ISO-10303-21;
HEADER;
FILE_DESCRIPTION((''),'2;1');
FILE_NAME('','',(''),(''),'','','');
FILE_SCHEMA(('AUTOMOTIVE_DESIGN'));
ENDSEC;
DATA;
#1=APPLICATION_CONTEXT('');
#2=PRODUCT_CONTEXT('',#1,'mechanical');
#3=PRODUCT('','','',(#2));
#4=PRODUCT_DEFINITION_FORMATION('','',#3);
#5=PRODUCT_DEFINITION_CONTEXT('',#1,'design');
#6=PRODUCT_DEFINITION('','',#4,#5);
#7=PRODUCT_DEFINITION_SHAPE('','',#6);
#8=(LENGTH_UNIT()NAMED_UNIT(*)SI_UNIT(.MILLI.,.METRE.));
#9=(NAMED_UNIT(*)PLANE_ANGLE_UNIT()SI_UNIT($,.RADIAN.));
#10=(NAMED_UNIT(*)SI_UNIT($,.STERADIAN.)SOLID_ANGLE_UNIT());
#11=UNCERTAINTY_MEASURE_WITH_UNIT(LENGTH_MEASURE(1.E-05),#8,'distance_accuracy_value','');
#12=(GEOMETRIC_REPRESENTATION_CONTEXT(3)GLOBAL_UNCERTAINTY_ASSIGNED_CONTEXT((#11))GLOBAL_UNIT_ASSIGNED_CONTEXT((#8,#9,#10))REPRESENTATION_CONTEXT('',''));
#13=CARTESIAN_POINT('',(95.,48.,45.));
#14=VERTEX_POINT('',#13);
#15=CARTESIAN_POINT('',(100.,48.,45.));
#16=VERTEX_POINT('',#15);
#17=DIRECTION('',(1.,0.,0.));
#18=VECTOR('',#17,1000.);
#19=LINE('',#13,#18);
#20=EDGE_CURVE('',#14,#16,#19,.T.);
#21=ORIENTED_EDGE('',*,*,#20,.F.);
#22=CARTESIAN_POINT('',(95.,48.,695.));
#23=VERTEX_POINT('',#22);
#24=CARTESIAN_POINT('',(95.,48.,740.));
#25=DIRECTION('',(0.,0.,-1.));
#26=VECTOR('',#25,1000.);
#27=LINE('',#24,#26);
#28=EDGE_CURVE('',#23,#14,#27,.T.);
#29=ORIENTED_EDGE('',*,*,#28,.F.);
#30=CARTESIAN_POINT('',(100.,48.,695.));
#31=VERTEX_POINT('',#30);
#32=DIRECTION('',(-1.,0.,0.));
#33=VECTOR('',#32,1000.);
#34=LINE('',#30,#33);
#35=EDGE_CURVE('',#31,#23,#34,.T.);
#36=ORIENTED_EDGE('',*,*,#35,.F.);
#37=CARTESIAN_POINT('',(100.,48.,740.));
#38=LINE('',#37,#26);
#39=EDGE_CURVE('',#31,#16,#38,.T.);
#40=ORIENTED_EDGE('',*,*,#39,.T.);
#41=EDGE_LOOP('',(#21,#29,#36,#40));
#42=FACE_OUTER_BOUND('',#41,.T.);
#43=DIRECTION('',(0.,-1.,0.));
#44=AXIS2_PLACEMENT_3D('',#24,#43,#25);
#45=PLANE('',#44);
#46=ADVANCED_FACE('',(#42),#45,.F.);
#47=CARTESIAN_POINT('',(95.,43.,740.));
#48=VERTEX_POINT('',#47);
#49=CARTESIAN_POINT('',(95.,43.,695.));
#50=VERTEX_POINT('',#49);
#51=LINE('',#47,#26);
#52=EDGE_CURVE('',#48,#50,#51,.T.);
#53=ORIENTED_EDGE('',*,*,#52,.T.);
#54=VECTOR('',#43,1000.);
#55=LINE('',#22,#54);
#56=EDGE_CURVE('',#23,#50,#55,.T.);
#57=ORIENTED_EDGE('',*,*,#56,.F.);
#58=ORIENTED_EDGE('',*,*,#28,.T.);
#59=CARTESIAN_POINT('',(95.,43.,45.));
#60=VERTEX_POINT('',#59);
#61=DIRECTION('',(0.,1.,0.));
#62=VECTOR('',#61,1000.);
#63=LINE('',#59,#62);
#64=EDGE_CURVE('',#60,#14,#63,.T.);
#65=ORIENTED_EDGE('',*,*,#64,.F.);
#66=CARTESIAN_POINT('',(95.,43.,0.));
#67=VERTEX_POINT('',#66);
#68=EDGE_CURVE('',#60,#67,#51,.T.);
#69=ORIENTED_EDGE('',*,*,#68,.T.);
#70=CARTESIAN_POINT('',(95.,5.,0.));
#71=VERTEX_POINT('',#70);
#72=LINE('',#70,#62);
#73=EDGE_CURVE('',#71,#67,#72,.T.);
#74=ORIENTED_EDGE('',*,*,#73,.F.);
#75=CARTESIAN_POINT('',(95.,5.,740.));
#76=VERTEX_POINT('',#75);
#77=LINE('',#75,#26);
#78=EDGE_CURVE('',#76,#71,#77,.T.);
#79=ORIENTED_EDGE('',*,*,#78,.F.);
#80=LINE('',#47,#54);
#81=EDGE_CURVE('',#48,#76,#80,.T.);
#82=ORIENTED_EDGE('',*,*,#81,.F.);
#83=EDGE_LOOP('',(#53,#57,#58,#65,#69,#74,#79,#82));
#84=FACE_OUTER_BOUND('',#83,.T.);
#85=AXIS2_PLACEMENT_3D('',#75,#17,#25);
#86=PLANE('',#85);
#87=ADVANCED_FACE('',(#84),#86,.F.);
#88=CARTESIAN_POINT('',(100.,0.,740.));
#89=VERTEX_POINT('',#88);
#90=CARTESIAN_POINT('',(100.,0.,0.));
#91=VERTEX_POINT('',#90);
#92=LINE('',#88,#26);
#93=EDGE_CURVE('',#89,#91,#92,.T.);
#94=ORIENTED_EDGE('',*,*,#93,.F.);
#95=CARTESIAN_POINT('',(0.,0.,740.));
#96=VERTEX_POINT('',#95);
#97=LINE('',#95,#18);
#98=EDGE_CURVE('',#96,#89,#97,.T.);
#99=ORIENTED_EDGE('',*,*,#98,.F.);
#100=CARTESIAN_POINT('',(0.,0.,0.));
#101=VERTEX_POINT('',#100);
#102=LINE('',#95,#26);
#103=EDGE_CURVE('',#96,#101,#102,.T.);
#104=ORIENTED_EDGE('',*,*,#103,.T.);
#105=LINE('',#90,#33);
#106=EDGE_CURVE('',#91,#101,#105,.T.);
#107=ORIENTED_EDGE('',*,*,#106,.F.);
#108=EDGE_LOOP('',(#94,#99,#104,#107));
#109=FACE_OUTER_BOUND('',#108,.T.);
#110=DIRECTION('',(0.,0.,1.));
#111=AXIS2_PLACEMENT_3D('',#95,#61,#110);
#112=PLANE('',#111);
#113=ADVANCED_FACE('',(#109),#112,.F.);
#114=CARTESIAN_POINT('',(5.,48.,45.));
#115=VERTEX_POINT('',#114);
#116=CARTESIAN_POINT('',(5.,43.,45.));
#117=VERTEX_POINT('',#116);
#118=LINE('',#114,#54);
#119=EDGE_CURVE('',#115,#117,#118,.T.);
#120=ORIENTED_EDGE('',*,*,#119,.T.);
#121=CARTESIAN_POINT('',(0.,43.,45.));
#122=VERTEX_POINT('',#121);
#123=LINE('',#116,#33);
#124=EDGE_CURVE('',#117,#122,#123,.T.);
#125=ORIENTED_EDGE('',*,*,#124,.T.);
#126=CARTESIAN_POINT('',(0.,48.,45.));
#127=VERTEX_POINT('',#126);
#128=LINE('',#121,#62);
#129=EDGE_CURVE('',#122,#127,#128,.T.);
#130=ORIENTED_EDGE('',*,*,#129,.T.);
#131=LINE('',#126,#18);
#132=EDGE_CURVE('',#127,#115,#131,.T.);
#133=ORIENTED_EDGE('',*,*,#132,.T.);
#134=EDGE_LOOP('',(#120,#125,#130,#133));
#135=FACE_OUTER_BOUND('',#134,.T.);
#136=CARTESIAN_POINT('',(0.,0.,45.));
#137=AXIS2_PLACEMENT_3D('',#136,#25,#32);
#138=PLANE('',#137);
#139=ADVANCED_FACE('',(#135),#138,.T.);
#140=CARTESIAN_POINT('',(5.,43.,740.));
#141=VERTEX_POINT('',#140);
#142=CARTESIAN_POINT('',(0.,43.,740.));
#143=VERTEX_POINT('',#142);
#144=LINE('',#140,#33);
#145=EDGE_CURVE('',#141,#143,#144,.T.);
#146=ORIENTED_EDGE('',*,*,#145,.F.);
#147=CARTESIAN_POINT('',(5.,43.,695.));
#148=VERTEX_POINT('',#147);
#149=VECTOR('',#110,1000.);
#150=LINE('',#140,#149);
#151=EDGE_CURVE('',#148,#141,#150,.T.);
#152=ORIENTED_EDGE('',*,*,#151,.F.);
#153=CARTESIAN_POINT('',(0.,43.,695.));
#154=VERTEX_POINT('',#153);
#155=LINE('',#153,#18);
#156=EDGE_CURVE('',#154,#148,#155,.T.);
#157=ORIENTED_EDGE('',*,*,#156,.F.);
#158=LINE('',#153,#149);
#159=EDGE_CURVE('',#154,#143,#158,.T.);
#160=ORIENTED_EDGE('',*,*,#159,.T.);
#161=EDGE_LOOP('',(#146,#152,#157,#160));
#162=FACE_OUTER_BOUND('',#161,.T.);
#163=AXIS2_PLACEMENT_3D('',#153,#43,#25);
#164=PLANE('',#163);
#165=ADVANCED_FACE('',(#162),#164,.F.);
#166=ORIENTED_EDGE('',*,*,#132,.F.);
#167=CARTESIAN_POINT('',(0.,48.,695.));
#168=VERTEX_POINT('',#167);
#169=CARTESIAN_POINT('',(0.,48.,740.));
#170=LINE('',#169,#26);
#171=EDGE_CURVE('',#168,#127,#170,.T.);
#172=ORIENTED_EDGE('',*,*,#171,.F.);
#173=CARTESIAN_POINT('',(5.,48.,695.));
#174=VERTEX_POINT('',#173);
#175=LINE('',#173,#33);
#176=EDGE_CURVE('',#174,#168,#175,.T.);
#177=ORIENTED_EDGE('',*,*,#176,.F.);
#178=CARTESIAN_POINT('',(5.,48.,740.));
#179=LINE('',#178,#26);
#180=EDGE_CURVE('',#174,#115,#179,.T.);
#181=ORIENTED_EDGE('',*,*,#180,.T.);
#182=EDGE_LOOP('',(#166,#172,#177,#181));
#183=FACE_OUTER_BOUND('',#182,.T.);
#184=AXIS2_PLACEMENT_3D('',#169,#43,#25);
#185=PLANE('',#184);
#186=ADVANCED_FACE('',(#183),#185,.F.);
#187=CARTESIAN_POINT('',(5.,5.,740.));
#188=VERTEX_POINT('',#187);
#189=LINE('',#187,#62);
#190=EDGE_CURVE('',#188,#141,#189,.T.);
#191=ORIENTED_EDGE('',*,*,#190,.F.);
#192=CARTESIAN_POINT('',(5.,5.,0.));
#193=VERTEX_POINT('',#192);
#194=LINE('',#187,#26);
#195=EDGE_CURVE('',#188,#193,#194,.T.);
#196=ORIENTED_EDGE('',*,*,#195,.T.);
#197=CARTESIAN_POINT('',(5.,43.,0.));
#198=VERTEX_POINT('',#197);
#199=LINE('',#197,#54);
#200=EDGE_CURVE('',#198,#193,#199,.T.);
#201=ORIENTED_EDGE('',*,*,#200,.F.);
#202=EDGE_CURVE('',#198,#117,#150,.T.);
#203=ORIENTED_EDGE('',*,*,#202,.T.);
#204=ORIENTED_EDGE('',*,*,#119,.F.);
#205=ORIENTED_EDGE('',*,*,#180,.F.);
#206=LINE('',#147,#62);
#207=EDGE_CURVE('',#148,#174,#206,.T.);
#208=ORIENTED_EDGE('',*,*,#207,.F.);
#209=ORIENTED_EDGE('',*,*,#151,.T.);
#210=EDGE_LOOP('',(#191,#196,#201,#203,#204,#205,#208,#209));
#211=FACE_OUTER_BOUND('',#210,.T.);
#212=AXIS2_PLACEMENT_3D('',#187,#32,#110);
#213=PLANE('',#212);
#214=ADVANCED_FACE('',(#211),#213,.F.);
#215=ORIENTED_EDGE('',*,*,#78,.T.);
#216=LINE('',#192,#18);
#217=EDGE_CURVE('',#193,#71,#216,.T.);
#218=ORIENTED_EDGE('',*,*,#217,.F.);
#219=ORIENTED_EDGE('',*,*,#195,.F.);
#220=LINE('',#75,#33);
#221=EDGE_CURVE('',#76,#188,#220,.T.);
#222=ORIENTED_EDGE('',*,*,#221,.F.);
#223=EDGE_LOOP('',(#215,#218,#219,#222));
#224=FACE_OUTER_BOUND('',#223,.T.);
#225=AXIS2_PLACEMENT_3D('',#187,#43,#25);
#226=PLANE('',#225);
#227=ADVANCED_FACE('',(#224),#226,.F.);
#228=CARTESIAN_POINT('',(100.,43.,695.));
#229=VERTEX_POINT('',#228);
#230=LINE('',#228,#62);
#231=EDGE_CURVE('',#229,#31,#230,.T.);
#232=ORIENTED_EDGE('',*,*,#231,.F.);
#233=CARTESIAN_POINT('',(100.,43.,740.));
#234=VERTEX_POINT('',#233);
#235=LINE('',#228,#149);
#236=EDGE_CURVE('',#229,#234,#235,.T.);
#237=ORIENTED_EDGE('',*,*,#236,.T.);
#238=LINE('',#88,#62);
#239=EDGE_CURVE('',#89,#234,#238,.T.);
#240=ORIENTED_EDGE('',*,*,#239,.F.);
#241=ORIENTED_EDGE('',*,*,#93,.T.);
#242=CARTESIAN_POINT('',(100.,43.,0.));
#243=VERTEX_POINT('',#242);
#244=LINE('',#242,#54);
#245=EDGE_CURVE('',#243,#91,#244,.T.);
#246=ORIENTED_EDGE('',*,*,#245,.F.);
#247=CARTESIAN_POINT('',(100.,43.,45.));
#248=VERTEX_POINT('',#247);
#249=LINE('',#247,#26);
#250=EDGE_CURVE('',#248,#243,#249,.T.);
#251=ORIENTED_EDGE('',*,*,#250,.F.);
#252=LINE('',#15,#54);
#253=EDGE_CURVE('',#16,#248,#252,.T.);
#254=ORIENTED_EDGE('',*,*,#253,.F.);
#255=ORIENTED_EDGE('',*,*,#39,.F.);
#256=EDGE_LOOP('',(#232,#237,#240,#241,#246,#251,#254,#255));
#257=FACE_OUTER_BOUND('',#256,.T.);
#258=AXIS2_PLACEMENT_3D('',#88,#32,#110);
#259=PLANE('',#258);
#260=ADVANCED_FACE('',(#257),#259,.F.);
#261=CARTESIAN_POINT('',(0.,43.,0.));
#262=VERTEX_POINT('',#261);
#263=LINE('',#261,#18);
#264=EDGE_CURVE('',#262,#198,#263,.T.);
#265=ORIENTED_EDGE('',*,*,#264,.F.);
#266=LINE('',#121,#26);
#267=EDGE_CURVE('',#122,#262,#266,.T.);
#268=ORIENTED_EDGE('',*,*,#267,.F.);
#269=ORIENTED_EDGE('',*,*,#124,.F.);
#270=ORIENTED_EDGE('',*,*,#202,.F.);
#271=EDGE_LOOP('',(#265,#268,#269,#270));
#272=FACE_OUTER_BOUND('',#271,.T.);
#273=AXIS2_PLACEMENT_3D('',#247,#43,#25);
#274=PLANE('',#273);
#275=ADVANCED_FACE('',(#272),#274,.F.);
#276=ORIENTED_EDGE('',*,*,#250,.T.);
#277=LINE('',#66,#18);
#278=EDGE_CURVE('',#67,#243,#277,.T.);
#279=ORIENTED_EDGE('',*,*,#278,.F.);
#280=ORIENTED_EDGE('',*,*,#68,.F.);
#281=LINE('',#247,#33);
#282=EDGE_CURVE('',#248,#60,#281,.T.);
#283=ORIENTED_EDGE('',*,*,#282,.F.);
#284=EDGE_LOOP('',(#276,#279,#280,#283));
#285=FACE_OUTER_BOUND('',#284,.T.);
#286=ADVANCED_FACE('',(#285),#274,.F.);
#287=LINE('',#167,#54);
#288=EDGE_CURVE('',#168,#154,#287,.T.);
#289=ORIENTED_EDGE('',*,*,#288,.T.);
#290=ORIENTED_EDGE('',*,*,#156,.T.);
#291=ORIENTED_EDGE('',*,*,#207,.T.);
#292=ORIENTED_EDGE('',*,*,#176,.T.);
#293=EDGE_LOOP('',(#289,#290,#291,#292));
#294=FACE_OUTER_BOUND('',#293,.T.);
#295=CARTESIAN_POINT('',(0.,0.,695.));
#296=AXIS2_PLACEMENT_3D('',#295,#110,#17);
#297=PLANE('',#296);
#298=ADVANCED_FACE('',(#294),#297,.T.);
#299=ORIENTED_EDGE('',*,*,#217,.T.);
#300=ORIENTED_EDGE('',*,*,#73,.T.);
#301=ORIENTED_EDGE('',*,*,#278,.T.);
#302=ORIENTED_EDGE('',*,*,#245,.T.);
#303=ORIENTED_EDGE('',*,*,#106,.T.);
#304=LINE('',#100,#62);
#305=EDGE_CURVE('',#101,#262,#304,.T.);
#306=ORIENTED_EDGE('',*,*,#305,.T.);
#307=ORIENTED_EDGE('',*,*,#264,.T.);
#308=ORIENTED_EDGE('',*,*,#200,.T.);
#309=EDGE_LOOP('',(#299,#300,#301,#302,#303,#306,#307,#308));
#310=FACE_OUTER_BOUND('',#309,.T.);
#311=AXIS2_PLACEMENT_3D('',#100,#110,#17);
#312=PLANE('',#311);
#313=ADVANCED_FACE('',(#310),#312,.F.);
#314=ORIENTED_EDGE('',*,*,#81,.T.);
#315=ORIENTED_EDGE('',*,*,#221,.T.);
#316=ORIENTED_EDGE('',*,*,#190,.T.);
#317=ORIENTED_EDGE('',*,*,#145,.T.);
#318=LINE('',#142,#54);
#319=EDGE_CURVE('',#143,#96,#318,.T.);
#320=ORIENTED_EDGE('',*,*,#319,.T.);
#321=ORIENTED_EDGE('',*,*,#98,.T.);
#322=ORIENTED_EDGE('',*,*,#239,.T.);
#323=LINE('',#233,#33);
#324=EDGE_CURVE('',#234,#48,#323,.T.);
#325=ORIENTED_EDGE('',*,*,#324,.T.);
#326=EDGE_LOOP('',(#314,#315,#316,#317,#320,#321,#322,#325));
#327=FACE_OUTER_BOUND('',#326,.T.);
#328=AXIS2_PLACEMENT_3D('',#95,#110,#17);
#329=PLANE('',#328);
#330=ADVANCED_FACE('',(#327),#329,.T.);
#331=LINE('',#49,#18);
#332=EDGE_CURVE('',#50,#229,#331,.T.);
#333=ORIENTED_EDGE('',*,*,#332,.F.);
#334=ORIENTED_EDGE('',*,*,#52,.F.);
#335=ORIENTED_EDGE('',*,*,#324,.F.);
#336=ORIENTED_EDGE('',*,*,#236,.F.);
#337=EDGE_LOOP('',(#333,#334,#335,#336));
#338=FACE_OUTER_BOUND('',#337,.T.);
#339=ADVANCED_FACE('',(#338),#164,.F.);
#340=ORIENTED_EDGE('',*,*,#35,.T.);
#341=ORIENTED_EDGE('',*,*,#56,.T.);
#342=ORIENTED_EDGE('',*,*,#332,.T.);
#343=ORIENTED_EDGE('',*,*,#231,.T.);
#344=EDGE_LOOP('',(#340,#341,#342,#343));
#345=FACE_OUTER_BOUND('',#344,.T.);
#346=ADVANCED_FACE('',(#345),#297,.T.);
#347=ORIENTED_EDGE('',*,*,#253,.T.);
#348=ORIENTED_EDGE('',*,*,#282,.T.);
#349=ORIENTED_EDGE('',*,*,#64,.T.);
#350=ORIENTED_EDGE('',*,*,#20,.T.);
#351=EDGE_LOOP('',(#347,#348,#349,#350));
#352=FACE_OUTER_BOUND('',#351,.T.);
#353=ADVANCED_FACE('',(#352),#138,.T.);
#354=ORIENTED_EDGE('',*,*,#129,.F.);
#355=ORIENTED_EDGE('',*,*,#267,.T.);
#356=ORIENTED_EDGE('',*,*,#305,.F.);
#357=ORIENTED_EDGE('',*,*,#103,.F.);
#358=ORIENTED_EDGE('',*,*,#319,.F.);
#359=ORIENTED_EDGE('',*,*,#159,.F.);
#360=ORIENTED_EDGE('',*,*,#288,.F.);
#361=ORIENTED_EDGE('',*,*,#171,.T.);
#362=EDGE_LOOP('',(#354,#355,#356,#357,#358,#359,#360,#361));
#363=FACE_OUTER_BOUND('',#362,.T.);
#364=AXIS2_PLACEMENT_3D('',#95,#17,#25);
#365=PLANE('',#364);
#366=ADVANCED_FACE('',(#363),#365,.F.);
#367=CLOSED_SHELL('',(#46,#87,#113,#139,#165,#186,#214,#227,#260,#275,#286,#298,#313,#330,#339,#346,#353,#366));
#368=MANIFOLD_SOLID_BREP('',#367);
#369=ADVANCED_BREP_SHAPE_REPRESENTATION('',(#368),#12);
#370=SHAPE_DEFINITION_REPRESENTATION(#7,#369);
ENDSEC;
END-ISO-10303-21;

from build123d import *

# Parameters (mm, degrees)
EXTRUDE_1_DEPTH     = 740
SKETCH_2_W          = 100
SKETCH_2_H          = 5
CUT_EXTRUDE_1_DEPTH = 45
SKETCH_3_W          = 100
SKETCH_3_H          = 5
CUT_EXTRUDE_2_DEPTH = 45
CUT_EXTRUDE_3_DEPTH = 25
CUT_EXTRUDE_4_DEPTH = 25
SKETCH_8_W          = 5
SKETCH_8_H          = 5
CUT_EXTRUDE_5_DEPTH = 25
SKETCH_9_W          = 5
SKETCH_9_H          = 5
CUT_EXTRUDE_6_DEPTH = 25
EXTRUDE_2_DEPTH     = 25
SKETCH_11_W         = 5
SKETCH_11_H         = 5
EXTRUDE_3_DEPTH     = 25
EXTRUDE_4_DEPTH     = 25
SKETCH_13_W         = 5
SKETCH_13_H         = 5
EXTRUDE_5_DEPTH     = 25


with BuildPart() as part:
    # 草图1 → 凸台-拉伸1 (new body)
    with BuildSketch(Plane.XY):
        Polygon((0, 0), (100, 0), (100, 48), (95, 48), (95, 5), (5, 5), (5, 48), (0, 48), align=None)
    extrude(amount=EXTRUDE_1_DEPTH)

    # 草图2 → 切除-拉伸1 (cut)
    with BuildSketch(Plane(origin=(0, 0, 0), x_dir=(-1, 0, 0), z_dir=(0, 0, -1))):
        with Locations((-50, 45.5)):
            Rectangle(SKETCH_2_W, SKETCH_2_H)
    extrude(amount=-CUT_EXTRUDE_1_DEPTH, mode=Mode.SUBTRACT)

    # 草图3 → 切除-拉伸2 (cut)
    with BuildSketch(Plane.XY.offset(740)):
        with Locations((50, 45.5)):
            Rectangle(SKETCH_3_W, SKETCH_3_H)
    extrude(amount=-CUT_EXTRUDE_2_DEPTH, mode=Mode.SUBTRACT)

    # 草图6 → 切除-拉伸3 (cut)
    with BuildSketch(Plane(origin=(0, 0, 0), x_dir=(-1, 0, 0), z_dir=(0, 0, -1))):
        Polygon((-95, 43), (-100, 43), (-100, 0), (0, 0), (0, 43), (-5, 43), (-5, 5), (-95, 5), align=None)
    extrude(amount=-CUT_EXTRUDE_3_DEPTH, mode=Mode.SUBTRACT)

    # 草图7 → 切除-拉伸4 (cut)
    with BuildSketch(Plane.XY.offset(740)):
        Polygon((100, 0), (100, 43), (95, 43), (95, 5), (5, 5), (5, 43), (0, 43), (0, 0), align=None)
    extrude(amount=-CUT_EXTRUDE_4_DEPTH, mode=Mode.SUBTRACT)

    # 草图8 → 切除-拉伸5 (cut)
    with BuildSketch(Plane.XY.offset(695)):
        with Locations((97.5, 45.5)):
            Rectangle(SKETCH_8_W, SKETCH_8_H)
        with Locations((2.5, 45.5)):
            Rectangle(SKETCH_8_W, SKETCH_8_H)
    extrude(amount=-CUT_EXTRUDE_5_DEPTH, mode=Mode.SUBTRACT)

    # 草图9 → 切除-拉伸6 (cut)
    with BuildSketch(Plane(origin=(0, 0, 45), x_dir=(-1, 0, 0), z_dir=(0, 0, -1))):
        with Locations((-2.5, 45.5)):
            Rectangle(SKETCH_9_W, SKETCH_9_H)
        with Locations((-97.5, 45.5)):
            Rectangle(SKETCH_9_W, SKETCH_9_H)
    extrude(amount=-CUT_EXTRUDE_6_DEPTH, mode=Mode.SUBTRACT)

    # 草图10 → 凸台-拉伸2 (add)
    with BuildSketch(Plane(origin=(0, 0, 25), x_dir=(-1, 0, 0), z_dir=(0, 0, -1))):
        Polygon((-95, 5), (-95, 43), (-100, 43), (-100, 0), (0, 0), (0, 43), (-5, 43), (-5, 5), align=None)
    extrude(amount=EXTRUDE_2_DEPTH)

    # 草图11 → 凸台-拉伸3 (add)
    with BuildSketch(Plane(origin=(0, 0, 70), x_dir=(-1, 0, 0), z_dir=(0, 0, -1))):
        with Locations((-2.5, 45.5)):
            Rectangle(SKETCH_11_W, SKETCH_11_H)
        with Locations((-97.5, 45.5)):
            Rectangle(SKETCH_11_W, SKETCH_11_H)
    extrude(amount=EXTRUDE_3_DEPTH)

    # 草图12 → 凸台-拉伸4 (add)
    with BuildSketch(Plane.XY.offset(715)):
        Polygon((0, 0), (100, 0), (100, 43), (95, 43), (95, 5), (5, 5), (5, 43), (0, 43), align=None)
    extrude(amount=EXTRUDE_4_DEPTH)

    # 草图13 → 凸台-拉伸5 (add)
    with BuildSketch(Plane.XY.offset(670)):
        with Locations((2.5, 45.5)):
            Rectangle(SKETCH_13_W, SKETCH_13_H)
        with Locations((97.5, 45.5)):
            Rectangle(SKETCH_13_W, SKETCH_13_H)
    extrude(amount=EXTRUDE_5_DEPTH)


solid = part.part
